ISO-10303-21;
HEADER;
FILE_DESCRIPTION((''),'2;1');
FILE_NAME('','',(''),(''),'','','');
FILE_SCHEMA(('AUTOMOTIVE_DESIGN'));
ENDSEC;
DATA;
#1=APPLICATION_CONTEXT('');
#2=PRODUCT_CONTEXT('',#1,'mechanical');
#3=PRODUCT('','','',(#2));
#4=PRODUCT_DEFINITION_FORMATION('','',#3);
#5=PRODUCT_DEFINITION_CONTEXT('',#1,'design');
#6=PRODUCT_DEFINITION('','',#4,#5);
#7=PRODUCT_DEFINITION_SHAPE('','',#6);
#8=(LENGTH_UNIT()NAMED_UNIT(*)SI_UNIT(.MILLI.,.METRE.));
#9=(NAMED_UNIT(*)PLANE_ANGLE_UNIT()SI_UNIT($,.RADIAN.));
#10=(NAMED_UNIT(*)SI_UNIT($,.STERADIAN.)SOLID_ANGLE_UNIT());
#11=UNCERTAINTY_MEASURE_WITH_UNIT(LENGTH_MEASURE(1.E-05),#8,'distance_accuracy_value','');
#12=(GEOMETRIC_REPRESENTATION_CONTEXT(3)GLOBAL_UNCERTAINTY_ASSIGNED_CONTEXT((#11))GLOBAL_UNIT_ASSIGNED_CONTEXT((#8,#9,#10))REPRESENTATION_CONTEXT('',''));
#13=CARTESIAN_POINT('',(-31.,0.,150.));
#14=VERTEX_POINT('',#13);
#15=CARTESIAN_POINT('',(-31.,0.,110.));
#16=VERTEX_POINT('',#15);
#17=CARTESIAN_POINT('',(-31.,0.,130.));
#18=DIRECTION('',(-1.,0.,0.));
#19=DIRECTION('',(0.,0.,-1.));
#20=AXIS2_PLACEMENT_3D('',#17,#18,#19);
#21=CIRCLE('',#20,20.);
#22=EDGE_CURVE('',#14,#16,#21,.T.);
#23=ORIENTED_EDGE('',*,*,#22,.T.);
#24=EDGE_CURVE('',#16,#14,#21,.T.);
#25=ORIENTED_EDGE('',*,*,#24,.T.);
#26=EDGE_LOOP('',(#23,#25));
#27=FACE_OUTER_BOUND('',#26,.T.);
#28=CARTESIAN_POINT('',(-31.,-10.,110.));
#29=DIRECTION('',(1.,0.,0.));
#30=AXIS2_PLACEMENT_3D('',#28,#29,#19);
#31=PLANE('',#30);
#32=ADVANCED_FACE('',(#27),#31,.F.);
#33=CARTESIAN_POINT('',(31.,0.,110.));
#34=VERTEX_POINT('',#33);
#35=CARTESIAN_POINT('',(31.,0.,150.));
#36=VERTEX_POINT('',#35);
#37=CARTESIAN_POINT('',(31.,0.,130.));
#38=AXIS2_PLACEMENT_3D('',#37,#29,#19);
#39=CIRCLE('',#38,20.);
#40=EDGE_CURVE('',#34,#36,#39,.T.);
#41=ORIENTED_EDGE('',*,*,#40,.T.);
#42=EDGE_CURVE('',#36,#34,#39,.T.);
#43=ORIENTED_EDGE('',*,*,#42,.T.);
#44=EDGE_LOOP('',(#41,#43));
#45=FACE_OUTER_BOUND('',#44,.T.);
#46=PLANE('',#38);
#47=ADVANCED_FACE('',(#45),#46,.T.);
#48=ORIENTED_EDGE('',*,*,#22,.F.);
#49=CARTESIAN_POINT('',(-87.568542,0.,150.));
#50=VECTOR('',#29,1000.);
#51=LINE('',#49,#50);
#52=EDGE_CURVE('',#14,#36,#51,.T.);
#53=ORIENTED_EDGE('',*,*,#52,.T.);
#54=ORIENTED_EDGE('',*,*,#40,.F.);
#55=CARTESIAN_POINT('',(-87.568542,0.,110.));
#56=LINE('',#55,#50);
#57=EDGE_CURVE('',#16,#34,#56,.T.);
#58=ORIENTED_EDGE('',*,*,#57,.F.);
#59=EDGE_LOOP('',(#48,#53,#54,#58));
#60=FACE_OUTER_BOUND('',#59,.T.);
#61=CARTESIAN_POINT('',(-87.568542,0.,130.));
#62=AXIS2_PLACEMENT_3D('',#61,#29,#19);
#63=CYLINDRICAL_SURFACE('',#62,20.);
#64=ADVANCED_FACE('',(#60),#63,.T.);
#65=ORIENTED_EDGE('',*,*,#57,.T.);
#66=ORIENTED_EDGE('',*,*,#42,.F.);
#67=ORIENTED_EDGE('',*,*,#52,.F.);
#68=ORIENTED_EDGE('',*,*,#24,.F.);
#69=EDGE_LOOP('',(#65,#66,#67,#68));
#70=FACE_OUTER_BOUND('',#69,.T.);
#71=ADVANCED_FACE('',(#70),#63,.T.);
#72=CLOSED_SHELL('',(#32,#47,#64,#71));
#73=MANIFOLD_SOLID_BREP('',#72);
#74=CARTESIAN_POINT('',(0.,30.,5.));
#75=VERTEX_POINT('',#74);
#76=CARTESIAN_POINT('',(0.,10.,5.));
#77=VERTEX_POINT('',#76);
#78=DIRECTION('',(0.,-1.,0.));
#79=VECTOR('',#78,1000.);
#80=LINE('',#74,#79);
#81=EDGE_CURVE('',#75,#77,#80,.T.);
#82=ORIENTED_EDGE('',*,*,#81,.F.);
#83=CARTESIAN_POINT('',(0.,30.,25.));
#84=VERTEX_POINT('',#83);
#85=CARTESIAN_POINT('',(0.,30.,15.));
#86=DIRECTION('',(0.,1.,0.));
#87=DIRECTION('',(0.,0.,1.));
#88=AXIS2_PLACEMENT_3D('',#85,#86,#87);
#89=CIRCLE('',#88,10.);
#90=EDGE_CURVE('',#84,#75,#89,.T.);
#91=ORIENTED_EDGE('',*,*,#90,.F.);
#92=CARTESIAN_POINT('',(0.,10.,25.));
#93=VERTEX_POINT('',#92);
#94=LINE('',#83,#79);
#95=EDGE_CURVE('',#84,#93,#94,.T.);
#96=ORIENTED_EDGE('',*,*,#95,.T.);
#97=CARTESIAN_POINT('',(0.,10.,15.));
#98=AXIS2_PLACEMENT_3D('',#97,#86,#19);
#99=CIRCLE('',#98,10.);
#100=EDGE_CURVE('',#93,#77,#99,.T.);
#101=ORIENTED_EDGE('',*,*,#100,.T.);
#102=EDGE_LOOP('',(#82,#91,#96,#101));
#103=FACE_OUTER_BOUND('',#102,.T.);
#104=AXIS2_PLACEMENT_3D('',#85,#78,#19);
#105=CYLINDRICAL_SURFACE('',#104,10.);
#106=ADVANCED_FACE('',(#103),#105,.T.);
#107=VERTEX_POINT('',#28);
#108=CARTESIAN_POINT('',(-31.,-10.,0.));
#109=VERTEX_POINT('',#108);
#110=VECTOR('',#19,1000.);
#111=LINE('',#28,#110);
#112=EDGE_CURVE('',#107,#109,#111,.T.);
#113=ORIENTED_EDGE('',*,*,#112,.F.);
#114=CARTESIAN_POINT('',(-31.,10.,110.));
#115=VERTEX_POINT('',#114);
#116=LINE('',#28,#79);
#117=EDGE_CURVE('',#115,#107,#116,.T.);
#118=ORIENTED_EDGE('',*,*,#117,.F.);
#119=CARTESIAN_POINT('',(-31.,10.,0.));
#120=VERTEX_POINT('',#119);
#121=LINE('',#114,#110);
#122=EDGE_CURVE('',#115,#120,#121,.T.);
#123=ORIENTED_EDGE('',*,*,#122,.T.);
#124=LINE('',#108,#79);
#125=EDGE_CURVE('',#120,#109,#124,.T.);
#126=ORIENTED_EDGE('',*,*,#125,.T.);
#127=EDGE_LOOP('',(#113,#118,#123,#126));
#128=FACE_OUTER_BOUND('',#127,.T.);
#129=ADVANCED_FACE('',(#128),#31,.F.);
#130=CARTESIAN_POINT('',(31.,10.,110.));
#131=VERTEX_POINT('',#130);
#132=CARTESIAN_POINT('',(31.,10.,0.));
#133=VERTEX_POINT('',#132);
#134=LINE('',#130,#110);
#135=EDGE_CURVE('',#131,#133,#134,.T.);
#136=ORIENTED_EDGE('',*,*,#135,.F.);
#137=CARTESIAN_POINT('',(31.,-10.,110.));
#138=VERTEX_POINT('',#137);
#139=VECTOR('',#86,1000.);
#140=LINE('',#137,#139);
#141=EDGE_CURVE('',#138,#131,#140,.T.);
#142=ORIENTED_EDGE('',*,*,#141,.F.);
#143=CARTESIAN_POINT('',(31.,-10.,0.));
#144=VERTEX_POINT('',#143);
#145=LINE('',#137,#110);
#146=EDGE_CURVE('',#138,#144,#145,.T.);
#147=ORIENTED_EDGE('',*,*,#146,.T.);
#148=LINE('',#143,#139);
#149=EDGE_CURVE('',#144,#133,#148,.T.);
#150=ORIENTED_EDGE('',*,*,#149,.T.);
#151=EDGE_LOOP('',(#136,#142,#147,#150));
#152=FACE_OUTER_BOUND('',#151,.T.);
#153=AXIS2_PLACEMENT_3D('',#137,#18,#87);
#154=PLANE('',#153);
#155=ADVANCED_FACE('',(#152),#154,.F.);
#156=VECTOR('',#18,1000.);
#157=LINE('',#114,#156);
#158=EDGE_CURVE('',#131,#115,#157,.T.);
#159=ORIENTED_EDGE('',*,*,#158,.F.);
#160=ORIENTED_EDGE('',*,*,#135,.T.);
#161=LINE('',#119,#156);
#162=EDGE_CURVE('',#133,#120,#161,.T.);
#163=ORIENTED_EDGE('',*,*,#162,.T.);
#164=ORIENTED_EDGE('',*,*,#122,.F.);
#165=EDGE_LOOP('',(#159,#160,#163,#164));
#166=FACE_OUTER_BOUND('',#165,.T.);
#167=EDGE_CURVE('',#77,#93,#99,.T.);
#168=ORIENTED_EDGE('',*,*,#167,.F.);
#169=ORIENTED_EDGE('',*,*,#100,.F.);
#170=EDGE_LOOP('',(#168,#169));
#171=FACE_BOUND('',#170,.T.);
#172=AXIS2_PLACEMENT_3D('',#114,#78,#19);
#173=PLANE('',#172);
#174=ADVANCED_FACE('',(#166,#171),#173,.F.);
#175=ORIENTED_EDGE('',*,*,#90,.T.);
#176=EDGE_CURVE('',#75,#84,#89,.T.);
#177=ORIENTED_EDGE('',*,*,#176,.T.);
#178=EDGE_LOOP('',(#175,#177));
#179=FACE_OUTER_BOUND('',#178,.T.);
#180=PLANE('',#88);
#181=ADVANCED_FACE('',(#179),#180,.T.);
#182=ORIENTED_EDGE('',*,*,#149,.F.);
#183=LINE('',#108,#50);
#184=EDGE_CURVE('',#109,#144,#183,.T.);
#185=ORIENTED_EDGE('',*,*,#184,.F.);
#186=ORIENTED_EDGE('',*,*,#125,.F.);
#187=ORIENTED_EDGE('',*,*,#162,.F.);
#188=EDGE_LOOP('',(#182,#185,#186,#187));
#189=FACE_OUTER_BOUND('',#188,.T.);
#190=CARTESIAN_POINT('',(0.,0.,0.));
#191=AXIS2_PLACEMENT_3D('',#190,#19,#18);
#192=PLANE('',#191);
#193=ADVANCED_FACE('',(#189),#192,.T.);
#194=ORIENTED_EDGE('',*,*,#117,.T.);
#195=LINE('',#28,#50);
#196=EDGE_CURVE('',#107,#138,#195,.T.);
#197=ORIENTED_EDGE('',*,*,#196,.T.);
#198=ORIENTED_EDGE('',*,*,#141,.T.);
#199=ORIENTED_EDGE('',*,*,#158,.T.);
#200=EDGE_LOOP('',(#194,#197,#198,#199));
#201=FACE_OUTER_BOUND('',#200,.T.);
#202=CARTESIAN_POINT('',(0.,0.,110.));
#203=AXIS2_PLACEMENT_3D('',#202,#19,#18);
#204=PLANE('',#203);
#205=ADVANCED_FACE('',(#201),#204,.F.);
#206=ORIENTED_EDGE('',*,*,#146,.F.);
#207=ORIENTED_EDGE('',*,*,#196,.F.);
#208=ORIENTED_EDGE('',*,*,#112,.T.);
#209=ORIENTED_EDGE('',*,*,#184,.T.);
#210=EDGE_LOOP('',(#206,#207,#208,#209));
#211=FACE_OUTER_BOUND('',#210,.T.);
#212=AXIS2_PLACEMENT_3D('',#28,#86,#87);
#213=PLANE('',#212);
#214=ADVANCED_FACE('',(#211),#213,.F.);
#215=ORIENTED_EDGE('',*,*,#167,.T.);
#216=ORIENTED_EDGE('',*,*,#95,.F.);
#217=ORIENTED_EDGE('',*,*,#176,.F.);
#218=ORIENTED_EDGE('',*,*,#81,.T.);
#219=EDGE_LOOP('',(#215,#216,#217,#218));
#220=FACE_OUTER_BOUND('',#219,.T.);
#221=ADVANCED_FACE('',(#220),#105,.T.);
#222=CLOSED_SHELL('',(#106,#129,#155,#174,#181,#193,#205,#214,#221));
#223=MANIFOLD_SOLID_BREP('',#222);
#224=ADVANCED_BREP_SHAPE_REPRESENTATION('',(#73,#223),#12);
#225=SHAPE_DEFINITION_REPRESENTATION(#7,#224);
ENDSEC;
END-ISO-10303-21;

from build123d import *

# Parameters (mm, degrees)
SKETCH_1_W      = 62
SKETCH_1_H      = 20
EXTRUDE_1_DEPTH = 110
SKETCH_2_R      = 20
EXTRUDE_2_DEPTH = 62
SKETCH_3_R      = 10
EXTRUDE_3_DEPTH = 20


with BuildPart() as part:
    # 草图1 → 凸台-拉伸1 (new body)
    with BuildSketch(Plane.XY):
        Rectangle(SKETCH_1_W, SKETCH_1_H)
    extrude(amount=EXTRUDE_1_DEPTH)

    # 草图3 → 凸台-拉伸3 (add)
    with BuildSketch(Plane(origin=(0, 10, 0), x_dir=(1, 0, 0), z_dir=(0, 1, 0))):
        with Locations(Location((0, -15, 0), (0, 0, 90))):
            Circle(SKETCH_3_R)
    extrude(amount=EXTRUDE_3_DEPTH)


with BuildPart() as body_2:
    # 草图2 → 凸台-拉伸2 (new body)
    with BuildSketch(Plane(origin=(31, 0, 0), x_dir=(0, 0, -1), z_dir=(1, 0, 0))):
        with Locations((-130, 0)):
            Circle(SKETCH_2_R)
    extrude(amount=-EXTRUDE_2_DEPTH)


solid = Compound([part.part, body_2.part])
